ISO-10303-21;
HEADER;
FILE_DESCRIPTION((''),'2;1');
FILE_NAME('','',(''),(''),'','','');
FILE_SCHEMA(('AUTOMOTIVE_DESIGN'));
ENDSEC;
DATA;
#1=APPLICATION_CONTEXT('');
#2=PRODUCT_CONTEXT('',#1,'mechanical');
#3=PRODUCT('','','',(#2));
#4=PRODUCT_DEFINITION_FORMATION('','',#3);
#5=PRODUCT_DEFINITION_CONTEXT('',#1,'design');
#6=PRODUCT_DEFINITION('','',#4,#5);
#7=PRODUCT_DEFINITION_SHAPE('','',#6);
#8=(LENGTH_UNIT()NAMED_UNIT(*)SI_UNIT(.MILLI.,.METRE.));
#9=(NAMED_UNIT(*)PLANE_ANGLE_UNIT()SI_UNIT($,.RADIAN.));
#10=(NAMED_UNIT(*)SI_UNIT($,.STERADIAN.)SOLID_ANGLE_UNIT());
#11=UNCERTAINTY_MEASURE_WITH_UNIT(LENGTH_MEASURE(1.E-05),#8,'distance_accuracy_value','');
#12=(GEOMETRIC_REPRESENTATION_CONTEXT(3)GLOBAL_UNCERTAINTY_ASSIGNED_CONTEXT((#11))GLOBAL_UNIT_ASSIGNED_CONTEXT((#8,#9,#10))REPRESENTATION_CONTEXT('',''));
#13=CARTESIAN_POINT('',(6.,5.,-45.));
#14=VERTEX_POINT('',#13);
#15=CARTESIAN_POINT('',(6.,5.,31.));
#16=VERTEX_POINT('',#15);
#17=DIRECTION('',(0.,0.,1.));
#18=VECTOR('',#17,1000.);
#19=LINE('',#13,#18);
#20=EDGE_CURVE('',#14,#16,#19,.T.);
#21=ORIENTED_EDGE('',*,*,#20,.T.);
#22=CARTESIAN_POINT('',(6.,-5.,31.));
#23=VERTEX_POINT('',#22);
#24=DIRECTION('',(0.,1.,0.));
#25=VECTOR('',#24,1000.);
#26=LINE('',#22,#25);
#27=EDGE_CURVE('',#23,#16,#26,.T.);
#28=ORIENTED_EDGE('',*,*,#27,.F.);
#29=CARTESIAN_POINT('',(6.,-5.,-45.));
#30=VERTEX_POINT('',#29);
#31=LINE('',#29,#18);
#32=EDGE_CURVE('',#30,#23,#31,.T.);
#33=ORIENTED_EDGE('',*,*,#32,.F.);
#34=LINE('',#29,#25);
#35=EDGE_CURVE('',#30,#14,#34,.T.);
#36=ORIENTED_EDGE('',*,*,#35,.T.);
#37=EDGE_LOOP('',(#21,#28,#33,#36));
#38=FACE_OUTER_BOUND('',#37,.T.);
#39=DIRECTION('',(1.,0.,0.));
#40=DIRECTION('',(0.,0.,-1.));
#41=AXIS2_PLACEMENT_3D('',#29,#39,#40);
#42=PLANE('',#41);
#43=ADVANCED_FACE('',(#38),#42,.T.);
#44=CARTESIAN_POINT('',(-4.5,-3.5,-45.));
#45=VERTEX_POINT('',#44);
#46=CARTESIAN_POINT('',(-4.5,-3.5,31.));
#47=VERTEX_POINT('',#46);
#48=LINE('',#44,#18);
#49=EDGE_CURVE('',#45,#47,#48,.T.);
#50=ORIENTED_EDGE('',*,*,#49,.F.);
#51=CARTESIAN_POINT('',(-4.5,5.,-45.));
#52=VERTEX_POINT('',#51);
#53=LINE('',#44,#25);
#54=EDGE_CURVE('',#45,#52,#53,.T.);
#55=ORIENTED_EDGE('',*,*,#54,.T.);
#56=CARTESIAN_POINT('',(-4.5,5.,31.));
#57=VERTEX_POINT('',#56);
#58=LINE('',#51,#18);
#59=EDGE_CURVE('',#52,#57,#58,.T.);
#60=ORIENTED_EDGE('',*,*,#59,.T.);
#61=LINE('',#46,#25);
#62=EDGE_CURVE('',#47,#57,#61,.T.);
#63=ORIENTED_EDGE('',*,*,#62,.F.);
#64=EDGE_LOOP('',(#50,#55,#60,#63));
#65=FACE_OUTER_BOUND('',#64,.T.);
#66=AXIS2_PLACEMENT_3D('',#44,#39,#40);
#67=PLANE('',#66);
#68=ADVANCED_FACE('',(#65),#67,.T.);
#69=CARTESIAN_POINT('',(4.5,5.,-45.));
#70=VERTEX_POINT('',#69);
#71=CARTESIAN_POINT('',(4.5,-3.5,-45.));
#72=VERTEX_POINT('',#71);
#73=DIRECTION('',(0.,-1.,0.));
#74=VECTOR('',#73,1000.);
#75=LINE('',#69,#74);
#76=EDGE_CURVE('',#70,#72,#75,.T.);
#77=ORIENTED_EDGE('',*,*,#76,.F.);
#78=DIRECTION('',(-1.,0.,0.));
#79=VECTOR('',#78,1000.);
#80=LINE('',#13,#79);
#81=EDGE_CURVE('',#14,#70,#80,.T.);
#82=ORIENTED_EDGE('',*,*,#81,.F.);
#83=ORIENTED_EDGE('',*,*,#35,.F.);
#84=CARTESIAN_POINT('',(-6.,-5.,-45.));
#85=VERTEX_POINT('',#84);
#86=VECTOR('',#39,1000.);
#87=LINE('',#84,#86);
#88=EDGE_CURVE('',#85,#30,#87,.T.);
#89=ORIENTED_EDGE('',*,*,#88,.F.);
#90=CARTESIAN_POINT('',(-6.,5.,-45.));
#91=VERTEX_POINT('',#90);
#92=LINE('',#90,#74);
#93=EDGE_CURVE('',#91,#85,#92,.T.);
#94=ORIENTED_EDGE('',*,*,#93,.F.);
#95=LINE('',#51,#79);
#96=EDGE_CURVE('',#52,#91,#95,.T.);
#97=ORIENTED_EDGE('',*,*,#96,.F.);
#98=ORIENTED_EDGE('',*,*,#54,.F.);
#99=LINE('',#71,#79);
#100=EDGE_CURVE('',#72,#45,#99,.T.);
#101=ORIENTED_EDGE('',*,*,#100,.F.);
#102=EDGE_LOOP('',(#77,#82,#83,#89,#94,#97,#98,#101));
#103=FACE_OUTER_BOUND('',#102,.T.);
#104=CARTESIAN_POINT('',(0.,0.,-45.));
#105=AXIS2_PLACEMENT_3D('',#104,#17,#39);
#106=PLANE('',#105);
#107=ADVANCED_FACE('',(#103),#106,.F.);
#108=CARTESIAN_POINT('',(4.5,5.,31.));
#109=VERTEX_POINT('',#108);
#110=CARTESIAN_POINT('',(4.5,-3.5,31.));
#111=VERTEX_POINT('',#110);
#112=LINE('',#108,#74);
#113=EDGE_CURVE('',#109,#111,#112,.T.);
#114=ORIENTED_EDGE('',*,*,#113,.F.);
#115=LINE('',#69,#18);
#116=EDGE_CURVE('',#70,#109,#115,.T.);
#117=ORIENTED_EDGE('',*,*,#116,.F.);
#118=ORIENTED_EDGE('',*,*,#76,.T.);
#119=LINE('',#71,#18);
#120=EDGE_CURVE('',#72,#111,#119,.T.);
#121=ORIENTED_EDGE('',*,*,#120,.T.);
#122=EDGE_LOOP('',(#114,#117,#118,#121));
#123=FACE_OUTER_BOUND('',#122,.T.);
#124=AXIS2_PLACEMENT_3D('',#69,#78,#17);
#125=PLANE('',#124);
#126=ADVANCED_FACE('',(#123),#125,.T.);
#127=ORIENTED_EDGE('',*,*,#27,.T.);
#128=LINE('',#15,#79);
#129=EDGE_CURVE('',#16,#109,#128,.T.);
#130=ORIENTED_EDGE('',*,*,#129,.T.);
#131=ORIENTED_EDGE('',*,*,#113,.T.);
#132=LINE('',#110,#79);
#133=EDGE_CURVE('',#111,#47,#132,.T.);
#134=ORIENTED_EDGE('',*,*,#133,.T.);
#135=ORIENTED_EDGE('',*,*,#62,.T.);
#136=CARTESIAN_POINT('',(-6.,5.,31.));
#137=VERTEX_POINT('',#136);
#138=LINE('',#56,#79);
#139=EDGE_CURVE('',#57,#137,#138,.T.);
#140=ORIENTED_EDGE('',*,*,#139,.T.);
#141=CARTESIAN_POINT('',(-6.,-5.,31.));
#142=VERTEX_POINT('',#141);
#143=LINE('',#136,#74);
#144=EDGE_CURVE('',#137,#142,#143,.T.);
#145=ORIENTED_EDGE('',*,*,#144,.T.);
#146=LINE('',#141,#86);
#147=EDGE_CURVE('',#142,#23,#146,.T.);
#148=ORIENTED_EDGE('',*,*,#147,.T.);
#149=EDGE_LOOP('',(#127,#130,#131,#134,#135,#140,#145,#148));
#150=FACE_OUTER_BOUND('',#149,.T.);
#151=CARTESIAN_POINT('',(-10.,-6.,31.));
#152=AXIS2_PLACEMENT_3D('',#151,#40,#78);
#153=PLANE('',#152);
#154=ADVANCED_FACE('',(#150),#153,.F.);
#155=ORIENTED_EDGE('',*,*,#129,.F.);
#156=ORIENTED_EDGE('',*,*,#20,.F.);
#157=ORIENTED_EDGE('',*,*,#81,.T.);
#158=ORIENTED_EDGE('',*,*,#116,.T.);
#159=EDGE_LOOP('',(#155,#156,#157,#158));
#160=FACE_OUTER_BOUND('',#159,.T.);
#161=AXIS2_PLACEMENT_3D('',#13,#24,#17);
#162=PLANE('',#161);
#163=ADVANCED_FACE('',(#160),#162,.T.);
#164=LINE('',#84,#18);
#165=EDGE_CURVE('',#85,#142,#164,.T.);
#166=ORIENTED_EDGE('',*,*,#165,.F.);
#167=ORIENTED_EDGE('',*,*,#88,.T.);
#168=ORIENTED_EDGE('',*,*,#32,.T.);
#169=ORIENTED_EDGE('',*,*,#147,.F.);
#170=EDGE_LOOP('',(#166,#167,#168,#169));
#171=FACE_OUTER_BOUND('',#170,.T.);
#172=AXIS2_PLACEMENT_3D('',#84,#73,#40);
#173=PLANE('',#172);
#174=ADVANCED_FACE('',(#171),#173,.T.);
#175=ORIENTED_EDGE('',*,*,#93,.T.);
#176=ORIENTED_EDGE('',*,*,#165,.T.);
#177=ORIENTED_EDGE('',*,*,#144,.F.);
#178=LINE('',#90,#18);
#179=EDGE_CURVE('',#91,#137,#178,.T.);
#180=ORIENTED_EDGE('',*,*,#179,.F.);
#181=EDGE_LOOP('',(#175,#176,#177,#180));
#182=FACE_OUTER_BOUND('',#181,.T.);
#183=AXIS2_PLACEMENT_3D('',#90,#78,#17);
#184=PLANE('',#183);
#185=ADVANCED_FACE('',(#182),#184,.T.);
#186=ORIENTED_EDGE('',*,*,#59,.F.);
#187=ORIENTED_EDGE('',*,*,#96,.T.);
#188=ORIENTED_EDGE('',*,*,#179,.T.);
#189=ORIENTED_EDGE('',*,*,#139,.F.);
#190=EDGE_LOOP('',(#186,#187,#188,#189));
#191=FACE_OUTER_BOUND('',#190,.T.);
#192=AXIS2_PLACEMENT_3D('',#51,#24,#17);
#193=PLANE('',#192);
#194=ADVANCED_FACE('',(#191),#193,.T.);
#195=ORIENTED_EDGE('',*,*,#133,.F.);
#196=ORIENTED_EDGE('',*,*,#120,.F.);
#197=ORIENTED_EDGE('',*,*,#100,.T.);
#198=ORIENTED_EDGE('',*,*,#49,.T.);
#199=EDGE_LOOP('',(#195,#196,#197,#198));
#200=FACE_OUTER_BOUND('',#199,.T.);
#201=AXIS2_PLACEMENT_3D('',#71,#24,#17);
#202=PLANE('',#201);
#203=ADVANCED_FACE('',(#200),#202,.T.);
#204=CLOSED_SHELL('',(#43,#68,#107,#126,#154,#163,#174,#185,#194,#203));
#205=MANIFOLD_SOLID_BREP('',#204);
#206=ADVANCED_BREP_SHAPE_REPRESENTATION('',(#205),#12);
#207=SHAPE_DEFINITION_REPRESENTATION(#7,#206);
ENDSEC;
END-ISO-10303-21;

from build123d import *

# Parameters (mm, degrees)
EXTRUDE_1_DEPTH     = 45
SKETCH_2_W          = 15
SKETCH_2_H          = 12
CUT_EXTRUDE_1_DEPTH = 10


with BuildPart() as part:
    # 草图1 → 凸台-拉伸1 (new, symmetric)
    with BuildSketch(Plane.XY):
        Polygon((-6, -5), (6, -5), (6, 5), (4.5, 5), (4.5, -3.5), (-4.5, -3.5), (-4.5, 5), (-6, 5), align=None)
    extrude(amount=EXTRUDE_1_DEPTH, both=True)

    # 草图2 → 切除-拉伸1 (cut, symmetric)
    with BuildSketch(Plane(origin=(0, 0, 0), x_dir=(0, 0, -1), z_dir=(1, 0, 0))):
        with Locations((-38.5, 0)):
            Rectangle(SKETCH_2_W, SKETCH_2_H)
    extrude(amount=CUT_EXTRUDE_1_DEPTH, both=True, mode=Mode.SUBTRACT)


solid = part.part
